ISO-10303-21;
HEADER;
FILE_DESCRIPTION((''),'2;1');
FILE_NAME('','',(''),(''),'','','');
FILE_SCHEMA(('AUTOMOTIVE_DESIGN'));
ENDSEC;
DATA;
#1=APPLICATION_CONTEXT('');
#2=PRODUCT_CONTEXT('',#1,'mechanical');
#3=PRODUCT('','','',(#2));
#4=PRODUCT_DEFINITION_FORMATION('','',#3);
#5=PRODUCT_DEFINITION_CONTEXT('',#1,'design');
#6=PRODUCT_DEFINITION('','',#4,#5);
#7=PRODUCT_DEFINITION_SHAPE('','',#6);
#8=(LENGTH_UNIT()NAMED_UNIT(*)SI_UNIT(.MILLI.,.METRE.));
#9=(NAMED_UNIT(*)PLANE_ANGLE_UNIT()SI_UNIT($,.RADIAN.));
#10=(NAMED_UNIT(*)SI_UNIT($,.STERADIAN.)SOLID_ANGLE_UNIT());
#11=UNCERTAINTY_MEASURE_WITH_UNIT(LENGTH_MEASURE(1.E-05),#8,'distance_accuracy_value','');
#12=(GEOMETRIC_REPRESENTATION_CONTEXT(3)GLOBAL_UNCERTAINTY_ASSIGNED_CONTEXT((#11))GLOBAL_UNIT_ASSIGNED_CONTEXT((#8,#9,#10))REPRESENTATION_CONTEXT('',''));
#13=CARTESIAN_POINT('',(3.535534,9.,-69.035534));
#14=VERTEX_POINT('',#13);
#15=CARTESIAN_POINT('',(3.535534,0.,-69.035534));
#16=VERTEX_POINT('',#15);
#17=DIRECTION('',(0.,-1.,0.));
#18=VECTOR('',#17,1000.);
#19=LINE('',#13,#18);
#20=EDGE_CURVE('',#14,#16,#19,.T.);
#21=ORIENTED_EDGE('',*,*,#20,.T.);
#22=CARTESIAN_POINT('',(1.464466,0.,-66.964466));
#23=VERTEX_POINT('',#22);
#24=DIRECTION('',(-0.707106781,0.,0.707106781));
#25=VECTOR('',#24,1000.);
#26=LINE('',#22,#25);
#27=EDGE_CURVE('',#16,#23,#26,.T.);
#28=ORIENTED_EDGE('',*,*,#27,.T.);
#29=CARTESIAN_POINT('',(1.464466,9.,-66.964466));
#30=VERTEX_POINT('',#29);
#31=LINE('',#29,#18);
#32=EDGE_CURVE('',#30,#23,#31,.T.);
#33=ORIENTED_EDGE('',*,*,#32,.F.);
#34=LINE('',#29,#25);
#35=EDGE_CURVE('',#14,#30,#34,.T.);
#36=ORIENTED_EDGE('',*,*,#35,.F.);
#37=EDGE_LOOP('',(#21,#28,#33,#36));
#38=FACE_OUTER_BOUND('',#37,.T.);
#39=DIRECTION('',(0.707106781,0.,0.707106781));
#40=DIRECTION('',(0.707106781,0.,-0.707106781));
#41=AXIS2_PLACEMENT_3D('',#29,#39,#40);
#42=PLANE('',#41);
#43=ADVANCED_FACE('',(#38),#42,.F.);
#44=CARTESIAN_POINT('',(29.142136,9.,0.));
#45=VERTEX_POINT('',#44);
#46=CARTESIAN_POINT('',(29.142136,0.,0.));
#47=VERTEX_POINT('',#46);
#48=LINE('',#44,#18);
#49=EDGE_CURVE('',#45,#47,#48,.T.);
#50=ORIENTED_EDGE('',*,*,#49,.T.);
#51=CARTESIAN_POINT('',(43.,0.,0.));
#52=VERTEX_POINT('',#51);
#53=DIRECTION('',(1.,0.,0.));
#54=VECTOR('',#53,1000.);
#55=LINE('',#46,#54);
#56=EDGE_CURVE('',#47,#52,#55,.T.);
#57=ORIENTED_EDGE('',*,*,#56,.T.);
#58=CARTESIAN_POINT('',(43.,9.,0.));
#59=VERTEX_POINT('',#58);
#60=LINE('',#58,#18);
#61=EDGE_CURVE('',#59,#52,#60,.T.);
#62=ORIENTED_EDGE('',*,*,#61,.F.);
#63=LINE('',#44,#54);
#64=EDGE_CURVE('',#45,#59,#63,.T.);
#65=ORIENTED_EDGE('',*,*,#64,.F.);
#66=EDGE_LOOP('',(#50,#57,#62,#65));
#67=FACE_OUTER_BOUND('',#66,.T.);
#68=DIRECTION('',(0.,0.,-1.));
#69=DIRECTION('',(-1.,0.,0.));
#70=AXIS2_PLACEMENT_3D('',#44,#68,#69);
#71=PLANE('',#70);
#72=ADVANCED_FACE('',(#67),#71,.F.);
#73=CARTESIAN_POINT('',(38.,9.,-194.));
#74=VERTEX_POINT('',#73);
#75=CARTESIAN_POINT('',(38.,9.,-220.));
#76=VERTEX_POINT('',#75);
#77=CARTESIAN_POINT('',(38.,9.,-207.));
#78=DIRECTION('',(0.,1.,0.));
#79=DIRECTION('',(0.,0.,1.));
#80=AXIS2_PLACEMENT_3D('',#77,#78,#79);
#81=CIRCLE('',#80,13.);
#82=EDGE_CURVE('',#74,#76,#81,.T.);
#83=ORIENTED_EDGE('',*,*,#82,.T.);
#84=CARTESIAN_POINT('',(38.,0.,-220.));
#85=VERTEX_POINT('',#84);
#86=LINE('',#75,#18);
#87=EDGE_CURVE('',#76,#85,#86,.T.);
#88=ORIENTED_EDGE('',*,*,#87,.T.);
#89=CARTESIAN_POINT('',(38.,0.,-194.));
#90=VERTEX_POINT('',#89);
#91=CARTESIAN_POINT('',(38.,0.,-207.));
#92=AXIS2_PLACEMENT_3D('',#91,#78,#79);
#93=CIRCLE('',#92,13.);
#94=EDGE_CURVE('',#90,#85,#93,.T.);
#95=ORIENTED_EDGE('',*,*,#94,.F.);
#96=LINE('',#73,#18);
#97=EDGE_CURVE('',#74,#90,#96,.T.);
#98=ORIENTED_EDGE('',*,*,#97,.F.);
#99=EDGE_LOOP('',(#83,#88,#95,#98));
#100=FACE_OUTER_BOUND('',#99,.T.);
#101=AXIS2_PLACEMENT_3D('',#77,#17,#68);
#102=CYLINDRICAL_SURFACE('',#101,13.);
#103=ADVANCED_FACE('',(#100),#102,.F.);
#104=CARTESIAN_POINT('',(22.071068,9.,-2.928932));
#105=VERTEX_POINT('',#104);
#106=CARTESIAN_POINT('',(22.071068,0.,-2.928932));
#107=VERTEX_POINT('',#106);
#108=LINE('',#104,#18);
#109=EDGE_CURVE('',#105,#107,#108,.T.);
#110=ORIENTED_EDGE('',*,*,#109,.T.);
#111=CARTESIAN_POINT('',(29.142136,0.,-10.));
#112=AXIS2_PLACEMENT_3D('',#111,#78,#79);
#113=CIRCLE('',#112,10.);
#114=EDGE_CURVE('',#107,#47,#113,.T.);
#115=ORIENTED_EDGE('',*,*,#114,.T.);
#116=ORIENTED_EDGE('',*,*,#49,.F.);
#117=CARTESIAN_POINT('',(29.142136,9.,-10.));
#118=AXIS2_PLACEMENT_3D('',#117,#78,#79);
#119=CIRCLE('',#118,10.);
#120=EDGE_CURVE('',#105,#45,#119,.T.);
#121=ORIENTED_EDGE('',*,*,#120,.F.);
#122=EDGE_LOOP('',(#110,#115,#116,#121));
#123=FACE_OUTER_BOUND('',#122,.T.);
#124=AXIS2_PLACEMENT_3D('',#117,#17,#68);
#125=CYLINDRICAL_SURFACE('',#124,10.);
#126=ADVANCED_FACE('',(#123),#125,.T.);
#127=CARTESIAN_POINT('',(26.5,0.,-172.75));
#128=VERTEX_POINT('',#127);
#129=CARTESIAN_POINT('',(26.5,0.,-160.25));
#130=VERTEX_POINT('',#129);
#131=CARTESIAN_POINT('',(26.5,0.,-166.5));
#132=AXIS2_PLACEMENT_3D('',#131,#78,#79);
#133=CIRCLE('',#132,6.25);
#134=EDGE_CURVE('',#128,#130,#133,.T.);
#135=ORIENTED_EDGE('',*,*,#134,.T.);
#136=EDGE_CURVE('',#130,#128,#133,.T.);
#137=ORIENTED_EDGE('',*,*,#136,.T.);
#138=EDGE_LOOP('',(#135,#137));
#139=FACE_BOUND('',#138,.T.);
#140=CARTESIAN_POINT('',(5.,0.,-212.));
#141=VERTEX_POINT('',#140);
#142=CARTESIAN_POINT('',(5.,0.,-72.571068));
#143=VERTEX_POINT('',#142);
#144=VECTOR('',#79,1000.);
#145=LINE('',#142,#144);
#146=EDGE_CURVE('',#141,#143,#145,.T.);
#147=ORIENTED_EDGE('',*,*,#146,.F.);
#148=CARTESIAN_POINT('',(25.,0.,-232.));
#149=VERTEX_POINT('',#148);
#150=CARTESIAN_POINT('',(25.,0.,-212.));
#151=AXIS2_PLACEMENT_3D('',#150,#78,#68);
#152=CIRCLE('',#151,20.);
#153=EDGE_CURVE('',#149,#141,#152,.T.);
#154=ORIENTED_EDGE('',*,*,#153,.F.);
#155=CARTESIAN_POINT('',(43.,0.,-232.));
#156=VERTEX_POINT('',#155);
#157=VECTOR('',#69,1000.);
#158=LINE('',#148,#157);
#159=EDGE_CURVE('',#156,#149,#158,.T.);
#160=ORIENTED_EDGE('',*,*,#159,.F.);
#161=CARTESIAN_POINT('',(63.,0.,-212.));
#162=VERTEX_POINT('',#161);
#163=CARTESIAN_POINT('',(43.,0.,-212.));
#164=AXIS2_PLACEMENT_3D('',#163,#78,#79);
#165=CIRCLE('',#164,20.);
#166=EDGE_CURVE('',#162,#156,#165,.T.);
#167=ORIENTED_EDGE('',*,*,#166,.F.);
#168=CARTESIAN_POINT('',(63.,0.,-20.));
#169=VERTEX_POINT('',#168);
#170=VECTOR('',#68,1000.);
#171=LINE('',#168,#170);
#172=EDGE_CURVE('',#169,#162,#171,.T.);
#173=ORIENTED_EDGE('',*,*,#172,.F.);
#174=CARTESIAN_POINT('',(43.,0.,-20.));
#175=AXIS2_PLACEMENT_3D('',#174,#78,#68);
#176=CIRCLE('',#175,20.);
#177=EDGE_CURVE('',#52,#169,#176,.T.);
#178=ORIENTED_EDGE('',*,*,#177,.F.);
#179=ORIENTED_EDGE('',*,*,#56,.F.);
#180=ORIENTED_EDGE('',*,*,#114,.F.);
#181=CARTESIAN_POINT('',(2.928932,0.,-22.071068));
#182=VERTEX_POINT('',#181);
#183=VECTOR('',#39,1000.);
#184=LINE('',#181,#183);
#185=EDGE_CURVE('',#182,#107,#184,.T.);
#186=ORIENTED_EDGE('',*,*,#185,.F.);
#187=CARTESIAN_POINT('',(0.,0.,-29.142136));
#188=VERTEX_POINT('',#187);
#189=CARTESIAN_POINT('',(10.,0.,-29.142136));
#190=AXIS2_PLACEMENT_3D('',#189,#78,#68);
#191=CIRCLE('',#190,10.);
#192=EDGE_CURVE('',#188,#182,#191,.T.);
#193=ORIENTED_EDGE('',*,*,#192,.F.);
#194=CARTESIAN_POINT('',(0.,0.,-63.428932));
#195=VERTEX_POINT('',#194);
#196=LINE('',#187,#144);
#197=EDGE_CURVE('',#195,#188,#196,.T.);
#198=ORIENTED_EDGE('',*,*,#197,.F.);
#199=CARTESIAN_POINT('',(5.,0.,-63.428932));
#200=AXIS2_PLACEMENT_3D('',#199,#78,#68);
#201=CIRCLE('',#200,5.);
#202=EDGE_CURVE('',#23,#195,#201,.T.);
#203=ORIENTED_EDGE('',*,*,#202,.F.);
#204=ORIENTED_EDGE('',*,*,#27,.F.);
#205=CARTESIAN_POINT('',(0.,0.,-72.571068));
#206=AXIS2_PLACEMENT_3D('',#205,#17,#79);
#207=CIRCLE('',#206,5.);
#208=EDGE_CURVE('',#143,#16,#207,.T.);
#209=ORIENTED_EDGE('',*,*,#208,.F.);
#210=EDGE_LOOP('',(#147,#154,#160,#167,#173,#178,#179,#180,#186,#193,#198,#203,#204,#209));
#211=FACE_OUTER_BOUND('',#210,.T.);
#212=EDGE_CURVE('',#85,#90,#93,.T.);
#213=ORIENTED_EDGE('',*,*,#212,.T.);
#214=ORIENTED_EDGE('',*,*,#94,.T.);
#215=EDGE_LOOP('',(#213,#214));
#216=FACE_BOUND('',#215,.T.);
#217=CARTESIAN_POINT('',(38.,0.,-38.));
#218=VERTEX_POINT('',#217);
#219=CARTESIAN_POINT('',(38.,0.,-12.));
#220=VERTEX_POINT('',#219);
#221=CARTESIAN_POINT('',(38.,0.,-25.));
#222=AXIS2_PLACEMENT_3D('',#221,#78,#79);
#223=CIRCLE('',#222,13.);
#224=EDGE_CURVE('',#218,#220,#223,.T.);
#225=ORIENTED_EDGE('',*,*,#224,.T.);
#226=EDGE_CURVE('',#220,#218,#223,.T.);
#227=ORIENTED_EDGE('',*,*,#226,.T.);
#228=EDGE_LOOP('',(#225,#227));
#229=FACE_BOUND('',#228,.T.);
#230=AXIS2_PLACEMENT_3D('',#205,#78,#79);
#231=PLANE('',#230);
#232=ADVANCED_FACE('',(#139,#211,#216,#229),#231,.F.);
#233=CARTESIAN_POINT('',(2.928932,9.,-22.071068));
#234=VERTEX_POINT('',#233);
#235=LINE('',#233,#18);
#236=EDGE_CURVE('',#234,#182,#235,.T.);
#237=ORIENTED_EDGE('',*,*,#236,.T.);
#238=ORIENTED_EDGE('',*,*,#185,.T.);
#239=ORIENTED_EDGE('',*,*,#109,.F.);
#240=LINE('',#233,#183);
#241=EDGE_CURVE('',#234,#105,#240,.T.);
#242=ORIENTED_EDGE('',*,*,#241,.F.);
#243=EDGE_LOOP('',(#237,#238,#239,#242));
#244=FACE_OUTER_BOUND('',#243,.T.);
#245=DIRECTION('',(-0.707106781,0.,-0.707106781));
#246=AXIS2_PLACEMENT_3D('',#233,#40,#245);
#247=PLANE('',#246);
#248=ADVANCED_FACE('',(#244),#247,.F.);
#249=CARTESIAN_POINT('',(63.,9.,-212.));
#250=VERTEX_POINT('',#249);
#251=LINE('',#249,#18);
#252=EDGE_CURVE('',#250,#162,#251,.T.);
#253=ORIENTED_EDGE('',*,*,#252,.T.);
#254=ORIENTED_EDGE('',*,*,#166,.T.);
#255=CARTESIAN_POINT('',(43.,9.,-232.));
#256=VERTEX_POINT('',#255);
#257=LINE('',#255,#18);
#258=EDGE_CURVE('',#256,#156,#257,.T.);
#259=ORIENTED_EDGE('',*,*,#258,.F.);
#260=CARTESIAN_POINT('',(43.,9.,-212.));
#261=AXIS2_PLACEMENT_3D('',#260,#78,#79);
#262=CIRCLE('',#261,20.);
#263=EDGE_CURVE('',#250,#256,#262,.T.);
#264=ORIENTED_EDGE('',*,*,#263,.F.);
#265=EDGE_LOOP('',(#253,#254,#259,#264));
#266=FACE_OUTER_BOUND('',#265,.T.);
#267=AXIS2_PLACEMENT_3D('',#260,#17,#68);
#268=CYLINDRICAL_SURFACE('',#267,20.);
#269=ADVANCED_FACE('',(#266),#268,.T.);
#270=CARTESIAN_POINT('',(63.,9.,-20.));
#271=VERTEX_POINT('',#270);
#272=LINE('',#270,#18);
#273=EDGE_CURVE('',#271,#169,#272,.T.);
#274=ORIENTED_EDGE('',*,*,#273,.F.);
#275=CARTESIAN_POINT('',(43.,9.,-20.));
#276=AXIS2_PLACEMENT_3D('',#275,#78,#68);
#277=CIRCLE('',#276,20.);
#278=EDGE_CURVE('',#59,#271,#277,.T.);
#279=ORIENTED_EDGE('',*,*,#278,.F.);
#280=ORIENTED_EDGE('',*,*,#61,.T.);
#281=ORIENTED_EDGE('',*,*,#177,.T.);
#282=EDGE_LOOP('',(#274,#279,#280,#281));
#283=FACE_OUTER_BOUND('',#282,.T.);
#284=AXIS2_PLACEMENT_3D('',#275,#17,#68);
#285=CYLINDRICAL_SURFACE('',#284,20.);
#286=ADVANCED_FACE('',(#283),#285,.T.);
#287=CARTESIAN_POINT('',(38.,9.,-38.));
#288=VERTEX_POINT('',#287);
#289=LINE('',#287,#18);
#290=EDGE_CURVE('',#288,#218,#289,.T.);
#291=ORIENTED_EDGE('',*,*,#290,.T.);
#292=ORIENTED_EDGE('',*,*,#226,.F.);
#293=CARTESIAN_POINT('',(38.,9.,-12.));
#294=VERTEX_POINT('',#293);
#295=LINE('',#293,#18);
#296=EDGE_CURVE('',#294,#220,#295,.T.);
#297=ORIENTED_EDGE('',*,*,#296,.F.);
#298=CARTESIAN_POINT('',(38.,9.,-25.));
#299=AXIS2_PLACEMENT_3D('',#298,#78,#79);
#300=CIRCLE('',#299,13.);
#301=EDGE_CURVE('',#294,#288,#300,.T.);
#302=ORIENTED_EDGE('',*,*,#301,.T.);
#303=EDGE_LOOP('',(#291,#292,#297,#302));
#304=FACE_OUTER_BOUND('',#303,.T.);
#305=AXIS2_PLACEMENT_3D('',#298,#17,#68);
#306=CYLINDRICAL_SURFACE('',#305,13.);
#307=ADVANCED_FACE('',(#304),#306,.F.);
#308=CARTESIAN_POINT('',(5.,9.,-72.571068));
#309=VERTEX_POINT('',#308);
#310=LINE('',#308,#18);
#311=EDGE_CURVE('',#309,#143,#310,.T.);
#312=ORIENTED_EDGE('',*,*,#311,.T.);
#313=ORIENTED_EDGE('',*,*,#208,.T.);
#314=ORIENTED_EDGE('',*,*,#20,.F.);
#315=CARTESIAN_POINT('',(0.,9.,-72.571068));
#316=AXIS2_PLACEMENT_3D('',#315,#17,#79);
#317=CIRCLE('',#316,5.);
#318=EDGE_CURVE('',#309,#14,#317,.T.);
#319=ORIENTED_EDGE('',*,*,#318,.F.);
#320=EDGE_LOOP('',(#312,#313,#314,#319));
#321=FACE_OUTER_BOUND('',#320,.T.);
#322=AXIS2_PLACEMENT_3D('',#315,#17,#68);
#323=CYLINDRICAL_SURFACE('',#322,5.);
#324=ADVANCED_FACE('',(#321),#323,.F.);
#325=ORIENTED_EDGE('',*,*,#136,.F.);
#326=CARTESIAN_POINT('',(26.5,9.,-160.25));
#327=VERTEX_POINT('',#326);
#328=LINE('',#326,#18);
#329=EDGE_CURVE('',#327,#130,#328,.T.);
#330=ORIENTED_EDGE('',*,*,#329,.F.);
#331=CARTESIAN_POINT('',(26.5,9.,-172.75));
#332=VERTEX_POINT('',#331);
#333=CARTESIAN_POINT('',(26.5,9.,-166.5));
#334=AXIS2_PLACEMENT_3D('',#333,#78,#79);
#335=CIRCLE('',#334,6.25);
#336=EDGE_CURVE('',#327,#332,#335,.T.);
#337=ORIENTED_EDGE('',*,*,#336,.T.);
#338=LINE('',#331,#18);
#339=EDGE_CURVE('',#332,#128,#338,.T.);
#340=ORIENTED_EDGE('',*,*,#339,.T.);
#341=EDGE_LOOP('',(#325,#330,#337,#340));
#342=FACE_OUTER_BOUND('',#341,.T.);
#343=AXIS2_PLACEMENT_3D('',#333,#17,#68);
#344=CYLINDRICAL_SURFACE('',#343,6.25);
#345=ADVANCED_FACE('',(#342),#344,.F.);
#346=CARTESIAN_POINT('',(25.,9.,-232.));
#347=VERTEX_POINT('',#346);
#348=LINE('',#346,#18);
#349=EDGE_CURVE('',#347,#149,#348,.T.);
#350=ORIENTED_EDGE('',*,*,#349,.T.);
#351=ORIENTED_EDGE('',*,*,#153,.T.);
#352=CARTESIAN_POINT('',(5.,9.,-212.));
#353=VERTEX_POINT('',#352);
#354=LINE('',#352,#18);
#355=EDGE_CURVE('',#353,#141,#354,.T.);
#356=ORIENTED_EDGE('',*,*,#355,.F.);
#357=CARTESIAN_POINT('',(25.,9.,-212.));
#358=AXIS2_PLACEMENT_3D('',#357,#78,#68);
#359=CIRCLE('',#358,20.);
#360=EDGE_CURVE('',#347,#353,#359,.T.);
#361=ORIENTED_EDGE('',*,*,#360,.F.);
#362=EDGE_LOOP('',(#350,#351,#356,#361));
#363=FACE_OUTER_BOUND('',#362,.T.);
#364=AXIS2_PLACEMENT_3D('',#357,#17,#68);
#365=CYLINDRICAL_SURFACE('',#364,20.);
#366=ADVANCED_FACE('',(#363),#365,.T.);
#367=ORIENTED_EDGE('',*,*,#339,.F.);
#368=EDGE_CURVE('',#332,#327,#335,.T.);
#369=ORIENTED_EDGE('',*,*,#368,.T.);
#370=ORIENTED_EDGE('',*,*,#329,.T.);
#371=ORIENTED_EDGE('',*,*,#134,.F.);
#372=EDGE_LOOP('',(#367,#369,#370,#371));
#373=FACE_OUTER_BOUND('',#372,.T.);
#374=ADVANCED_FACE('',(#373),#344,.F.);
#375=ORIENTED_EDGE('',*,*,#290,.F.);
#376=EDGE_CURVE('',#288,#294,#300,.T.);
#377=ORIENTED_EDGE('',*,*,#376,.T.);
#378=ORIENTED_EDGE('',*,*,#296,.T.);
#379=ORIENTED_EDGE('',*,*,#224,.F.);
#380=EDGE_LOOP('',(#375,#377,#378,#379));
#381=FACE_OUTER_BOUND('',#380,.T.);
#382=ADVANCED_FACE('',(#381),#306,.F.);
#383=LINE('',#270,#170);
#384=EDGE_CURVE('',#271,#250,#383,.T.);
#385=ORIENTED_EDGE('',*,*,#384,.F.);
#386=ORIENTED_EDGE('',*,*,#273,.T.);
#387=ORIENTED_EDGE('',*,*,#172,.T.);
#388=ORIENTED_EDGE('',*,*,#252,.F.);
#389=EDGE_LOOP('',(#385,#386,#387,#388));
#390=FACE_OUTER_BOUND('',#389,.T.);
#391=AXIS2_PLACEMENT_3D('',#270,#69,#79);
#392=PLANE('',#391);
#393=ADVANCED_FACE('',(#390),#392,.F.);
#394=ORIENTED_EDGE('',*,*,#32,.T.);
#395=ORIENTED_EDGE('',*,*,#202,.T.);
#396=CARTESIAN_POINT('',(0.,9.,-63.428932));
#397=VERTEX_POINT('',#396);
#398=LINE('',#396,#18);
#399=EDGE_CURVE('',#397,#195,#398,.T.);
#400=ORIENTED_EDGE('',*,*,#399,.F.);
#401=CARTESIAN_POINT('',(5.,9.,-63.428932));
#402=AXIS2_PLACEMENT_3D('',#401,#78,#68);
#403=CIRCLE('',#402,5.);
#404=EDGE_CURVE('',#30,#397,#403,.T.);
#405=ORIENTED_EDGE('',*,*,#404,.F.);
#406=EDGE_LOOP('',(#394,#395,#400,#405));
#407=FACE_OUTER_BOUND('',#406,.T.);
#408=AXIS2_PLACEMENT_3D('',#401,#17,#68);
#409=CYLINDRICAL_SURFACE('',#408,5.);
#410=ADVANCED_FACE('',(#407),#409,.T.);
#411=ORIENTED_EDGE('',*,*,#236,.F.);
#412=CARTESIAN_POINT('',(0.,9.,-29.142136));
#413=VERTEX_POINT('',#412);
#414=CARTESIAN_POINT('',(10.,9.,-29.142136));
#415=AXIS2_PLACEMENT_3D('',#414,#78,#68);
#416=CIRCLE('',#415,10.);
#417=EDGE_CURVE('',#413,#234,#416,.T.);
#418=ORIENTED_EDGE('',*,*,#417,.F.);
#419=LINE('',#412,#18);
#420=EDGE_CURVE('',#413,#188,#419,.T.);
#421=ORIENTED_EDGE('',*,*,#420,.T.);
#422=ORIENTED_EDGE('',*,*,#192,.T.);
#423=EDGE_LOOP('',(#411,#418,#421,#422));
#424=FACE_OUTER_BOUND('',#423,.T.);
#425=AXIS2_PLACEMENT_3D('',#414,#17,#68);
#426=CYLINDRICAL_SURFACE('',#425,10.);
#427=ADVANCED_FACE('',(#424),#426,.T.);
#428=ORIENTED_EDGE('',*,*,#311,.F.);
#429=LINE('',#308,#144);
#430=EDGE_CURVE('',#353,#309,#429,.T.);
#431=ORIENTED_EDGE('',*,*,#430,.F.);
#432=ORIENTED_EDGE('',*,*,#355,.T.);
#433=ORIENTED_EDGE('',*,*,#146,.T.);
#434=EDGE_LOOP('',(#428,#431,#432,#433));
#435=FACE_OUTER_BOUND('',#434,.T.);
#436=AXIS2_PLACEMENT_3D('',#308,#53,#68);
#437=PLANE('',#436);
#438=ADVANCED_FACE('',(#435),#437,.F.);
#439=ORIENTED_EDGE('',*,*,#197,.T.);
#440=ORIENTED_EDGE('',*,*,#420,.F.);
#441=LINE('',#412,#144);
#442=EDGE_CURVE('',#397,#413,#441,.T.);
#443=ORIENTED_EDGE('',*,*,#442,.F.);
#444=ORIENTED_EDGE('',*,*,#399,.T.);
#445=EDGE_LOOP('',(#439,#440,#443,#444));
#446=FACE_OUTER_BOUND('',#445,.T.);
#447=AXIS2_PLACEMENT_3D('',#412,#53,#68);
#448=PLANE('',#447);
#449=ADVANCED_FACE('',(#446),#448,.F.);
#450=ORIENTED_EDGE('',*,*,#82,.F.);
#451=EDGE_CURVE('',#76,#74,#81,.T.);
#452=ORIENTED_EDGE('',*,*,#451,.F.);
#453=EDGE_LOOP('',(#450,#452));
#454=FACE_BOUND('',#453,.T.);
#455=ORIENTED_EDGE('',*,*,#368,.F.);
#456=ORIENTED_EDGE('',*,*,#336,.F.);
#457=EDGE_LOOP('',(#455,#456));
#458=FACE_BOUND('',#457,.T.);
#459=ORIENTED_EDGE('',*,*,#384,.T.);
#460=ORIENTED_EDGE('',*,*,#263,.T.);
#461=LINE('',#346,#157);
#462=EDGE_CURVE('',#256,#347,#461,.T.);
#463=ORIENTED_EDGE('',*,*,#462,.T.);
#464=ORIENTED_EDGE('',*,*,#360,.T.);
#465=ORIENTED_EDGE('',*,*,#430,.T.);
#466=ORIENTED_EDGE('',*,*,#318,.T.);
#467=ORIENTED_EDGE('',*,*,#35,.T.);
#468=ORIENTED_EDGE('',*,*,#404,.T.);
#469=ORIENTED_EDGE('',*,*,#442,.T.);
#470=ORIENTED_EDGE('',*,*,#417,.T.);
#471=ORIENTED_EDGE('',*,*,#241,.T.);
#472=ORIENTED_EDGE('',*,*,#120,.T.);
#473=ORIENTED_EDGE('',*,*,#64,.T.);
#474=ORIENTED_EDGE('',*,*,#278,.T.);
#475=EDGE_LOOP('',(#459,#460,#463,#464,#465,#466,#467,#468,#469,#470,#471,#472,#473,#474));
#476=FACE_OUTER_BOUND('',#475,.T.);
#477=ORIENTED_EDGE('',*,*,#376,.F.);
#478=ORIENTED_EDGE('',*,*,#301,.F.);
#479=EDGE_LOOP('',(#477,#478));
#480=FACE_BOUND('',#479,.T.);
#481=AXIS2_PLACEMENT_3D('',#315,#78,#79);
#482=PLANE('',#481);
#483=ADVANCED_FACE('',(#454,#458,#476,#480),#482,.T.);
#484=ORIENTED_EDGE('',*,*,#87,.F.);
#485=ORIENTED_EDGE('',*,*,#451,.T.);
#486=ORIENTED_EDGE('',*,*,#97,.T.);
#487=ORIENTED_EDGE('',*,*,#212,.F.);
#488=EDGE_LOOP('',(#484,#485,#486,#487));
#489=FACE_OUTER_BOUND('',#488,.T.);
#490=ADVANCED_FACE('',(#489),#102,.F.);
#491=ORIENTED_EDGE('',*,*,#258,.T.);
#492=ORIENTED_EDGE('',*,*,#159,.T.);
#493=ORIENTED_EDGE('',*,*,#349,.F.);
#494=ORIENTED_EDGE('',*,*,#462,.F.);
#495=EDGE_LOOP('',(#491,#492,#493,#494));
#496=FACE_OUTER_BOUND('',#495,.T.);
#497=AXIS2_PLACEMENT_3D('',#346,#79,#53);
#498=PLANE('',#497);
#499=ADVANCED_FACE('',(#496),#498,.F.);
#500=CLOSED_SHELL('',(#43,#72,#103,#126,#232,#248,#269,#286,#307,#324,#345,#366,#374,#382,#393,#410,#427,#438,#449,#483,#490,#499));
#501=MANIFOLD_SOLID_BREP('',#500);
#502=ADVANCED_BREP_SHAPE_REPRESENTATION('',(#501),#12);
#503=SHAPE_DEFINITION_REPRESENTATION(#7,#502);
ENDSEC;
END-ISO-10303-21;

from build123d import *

# Parameters (mm, degrees)
SKETCH1_R           = 13
SKETCH1_R_2         = 6.25
BOSS_EXTRUDE1_DEPTH = 9


with BuildPart() as part:
    # Sketch1 → Boss-Extrude1 (new body)
    with BuildSketch(Plane(origin=(0, 0, 0), x_dir=(1, 0, 0), z_dir=(0, 1, 0))):
        with BuildLine():
            Line((2.928932188, 22.071067812), (22.071067812, 2.928932188))
            ThreePointArc((22.071067812, 2.928932188), (25.3153013, 0.761204675), (29.142135624, 0))
            Line((29.142135624, 0), (43, 0))
            ThreePointArc((43, 0), (57.142135624, 5.857864376), (63, 20))
            Line((63, 20), (63, 212))
            ThreePointArc((63, 212), (57.142135624, 226.142135624), (43, 232))
            Line((43, 232), (25, 232))
            ThreePointArc((25, 232), (10.857864376, 226.142135624), (5, 212))
            Line((5, 212), (5, 72.571067812))
            ThreePointArc((5, 72.571067812), (4.619397663, 70.65765065), (3.535533906, 69.035533906))
            Line((3.535533906, 69.035533906), (1.464466094, 66.964466094))
            ThreePointArc((1.464466094, 66.964466094), (0.380602337, 65.34234935), (0, 63.428932188))
            Line((0, 63.428932188), (0, 29.142135624))
            ThreePointArc((0, 29.142135624), (0.761204675, 25.3153013), (2.928932188, 22.071067812))
        make_face()
        with Locations(Location((38, 25, 0), (0, 0, 270))):
            Circle(SKETCH1_R, mode=Mode.SUBTRACT)
        with Locations(Location((38, 207, 0), (0, 0, 270))):
            Circle(SKETCH1_R, mode=Mode.SUBTRACT)
        with Locations(Location((26.5, 166.5, 0), (0, 0, 270))):
            Circle(SKETCH1_R_2, mode=Mode.SUBTRACT)
    extrude(amount=BOSS_EXTRUDE1_DEPTH)


solid = part.part
